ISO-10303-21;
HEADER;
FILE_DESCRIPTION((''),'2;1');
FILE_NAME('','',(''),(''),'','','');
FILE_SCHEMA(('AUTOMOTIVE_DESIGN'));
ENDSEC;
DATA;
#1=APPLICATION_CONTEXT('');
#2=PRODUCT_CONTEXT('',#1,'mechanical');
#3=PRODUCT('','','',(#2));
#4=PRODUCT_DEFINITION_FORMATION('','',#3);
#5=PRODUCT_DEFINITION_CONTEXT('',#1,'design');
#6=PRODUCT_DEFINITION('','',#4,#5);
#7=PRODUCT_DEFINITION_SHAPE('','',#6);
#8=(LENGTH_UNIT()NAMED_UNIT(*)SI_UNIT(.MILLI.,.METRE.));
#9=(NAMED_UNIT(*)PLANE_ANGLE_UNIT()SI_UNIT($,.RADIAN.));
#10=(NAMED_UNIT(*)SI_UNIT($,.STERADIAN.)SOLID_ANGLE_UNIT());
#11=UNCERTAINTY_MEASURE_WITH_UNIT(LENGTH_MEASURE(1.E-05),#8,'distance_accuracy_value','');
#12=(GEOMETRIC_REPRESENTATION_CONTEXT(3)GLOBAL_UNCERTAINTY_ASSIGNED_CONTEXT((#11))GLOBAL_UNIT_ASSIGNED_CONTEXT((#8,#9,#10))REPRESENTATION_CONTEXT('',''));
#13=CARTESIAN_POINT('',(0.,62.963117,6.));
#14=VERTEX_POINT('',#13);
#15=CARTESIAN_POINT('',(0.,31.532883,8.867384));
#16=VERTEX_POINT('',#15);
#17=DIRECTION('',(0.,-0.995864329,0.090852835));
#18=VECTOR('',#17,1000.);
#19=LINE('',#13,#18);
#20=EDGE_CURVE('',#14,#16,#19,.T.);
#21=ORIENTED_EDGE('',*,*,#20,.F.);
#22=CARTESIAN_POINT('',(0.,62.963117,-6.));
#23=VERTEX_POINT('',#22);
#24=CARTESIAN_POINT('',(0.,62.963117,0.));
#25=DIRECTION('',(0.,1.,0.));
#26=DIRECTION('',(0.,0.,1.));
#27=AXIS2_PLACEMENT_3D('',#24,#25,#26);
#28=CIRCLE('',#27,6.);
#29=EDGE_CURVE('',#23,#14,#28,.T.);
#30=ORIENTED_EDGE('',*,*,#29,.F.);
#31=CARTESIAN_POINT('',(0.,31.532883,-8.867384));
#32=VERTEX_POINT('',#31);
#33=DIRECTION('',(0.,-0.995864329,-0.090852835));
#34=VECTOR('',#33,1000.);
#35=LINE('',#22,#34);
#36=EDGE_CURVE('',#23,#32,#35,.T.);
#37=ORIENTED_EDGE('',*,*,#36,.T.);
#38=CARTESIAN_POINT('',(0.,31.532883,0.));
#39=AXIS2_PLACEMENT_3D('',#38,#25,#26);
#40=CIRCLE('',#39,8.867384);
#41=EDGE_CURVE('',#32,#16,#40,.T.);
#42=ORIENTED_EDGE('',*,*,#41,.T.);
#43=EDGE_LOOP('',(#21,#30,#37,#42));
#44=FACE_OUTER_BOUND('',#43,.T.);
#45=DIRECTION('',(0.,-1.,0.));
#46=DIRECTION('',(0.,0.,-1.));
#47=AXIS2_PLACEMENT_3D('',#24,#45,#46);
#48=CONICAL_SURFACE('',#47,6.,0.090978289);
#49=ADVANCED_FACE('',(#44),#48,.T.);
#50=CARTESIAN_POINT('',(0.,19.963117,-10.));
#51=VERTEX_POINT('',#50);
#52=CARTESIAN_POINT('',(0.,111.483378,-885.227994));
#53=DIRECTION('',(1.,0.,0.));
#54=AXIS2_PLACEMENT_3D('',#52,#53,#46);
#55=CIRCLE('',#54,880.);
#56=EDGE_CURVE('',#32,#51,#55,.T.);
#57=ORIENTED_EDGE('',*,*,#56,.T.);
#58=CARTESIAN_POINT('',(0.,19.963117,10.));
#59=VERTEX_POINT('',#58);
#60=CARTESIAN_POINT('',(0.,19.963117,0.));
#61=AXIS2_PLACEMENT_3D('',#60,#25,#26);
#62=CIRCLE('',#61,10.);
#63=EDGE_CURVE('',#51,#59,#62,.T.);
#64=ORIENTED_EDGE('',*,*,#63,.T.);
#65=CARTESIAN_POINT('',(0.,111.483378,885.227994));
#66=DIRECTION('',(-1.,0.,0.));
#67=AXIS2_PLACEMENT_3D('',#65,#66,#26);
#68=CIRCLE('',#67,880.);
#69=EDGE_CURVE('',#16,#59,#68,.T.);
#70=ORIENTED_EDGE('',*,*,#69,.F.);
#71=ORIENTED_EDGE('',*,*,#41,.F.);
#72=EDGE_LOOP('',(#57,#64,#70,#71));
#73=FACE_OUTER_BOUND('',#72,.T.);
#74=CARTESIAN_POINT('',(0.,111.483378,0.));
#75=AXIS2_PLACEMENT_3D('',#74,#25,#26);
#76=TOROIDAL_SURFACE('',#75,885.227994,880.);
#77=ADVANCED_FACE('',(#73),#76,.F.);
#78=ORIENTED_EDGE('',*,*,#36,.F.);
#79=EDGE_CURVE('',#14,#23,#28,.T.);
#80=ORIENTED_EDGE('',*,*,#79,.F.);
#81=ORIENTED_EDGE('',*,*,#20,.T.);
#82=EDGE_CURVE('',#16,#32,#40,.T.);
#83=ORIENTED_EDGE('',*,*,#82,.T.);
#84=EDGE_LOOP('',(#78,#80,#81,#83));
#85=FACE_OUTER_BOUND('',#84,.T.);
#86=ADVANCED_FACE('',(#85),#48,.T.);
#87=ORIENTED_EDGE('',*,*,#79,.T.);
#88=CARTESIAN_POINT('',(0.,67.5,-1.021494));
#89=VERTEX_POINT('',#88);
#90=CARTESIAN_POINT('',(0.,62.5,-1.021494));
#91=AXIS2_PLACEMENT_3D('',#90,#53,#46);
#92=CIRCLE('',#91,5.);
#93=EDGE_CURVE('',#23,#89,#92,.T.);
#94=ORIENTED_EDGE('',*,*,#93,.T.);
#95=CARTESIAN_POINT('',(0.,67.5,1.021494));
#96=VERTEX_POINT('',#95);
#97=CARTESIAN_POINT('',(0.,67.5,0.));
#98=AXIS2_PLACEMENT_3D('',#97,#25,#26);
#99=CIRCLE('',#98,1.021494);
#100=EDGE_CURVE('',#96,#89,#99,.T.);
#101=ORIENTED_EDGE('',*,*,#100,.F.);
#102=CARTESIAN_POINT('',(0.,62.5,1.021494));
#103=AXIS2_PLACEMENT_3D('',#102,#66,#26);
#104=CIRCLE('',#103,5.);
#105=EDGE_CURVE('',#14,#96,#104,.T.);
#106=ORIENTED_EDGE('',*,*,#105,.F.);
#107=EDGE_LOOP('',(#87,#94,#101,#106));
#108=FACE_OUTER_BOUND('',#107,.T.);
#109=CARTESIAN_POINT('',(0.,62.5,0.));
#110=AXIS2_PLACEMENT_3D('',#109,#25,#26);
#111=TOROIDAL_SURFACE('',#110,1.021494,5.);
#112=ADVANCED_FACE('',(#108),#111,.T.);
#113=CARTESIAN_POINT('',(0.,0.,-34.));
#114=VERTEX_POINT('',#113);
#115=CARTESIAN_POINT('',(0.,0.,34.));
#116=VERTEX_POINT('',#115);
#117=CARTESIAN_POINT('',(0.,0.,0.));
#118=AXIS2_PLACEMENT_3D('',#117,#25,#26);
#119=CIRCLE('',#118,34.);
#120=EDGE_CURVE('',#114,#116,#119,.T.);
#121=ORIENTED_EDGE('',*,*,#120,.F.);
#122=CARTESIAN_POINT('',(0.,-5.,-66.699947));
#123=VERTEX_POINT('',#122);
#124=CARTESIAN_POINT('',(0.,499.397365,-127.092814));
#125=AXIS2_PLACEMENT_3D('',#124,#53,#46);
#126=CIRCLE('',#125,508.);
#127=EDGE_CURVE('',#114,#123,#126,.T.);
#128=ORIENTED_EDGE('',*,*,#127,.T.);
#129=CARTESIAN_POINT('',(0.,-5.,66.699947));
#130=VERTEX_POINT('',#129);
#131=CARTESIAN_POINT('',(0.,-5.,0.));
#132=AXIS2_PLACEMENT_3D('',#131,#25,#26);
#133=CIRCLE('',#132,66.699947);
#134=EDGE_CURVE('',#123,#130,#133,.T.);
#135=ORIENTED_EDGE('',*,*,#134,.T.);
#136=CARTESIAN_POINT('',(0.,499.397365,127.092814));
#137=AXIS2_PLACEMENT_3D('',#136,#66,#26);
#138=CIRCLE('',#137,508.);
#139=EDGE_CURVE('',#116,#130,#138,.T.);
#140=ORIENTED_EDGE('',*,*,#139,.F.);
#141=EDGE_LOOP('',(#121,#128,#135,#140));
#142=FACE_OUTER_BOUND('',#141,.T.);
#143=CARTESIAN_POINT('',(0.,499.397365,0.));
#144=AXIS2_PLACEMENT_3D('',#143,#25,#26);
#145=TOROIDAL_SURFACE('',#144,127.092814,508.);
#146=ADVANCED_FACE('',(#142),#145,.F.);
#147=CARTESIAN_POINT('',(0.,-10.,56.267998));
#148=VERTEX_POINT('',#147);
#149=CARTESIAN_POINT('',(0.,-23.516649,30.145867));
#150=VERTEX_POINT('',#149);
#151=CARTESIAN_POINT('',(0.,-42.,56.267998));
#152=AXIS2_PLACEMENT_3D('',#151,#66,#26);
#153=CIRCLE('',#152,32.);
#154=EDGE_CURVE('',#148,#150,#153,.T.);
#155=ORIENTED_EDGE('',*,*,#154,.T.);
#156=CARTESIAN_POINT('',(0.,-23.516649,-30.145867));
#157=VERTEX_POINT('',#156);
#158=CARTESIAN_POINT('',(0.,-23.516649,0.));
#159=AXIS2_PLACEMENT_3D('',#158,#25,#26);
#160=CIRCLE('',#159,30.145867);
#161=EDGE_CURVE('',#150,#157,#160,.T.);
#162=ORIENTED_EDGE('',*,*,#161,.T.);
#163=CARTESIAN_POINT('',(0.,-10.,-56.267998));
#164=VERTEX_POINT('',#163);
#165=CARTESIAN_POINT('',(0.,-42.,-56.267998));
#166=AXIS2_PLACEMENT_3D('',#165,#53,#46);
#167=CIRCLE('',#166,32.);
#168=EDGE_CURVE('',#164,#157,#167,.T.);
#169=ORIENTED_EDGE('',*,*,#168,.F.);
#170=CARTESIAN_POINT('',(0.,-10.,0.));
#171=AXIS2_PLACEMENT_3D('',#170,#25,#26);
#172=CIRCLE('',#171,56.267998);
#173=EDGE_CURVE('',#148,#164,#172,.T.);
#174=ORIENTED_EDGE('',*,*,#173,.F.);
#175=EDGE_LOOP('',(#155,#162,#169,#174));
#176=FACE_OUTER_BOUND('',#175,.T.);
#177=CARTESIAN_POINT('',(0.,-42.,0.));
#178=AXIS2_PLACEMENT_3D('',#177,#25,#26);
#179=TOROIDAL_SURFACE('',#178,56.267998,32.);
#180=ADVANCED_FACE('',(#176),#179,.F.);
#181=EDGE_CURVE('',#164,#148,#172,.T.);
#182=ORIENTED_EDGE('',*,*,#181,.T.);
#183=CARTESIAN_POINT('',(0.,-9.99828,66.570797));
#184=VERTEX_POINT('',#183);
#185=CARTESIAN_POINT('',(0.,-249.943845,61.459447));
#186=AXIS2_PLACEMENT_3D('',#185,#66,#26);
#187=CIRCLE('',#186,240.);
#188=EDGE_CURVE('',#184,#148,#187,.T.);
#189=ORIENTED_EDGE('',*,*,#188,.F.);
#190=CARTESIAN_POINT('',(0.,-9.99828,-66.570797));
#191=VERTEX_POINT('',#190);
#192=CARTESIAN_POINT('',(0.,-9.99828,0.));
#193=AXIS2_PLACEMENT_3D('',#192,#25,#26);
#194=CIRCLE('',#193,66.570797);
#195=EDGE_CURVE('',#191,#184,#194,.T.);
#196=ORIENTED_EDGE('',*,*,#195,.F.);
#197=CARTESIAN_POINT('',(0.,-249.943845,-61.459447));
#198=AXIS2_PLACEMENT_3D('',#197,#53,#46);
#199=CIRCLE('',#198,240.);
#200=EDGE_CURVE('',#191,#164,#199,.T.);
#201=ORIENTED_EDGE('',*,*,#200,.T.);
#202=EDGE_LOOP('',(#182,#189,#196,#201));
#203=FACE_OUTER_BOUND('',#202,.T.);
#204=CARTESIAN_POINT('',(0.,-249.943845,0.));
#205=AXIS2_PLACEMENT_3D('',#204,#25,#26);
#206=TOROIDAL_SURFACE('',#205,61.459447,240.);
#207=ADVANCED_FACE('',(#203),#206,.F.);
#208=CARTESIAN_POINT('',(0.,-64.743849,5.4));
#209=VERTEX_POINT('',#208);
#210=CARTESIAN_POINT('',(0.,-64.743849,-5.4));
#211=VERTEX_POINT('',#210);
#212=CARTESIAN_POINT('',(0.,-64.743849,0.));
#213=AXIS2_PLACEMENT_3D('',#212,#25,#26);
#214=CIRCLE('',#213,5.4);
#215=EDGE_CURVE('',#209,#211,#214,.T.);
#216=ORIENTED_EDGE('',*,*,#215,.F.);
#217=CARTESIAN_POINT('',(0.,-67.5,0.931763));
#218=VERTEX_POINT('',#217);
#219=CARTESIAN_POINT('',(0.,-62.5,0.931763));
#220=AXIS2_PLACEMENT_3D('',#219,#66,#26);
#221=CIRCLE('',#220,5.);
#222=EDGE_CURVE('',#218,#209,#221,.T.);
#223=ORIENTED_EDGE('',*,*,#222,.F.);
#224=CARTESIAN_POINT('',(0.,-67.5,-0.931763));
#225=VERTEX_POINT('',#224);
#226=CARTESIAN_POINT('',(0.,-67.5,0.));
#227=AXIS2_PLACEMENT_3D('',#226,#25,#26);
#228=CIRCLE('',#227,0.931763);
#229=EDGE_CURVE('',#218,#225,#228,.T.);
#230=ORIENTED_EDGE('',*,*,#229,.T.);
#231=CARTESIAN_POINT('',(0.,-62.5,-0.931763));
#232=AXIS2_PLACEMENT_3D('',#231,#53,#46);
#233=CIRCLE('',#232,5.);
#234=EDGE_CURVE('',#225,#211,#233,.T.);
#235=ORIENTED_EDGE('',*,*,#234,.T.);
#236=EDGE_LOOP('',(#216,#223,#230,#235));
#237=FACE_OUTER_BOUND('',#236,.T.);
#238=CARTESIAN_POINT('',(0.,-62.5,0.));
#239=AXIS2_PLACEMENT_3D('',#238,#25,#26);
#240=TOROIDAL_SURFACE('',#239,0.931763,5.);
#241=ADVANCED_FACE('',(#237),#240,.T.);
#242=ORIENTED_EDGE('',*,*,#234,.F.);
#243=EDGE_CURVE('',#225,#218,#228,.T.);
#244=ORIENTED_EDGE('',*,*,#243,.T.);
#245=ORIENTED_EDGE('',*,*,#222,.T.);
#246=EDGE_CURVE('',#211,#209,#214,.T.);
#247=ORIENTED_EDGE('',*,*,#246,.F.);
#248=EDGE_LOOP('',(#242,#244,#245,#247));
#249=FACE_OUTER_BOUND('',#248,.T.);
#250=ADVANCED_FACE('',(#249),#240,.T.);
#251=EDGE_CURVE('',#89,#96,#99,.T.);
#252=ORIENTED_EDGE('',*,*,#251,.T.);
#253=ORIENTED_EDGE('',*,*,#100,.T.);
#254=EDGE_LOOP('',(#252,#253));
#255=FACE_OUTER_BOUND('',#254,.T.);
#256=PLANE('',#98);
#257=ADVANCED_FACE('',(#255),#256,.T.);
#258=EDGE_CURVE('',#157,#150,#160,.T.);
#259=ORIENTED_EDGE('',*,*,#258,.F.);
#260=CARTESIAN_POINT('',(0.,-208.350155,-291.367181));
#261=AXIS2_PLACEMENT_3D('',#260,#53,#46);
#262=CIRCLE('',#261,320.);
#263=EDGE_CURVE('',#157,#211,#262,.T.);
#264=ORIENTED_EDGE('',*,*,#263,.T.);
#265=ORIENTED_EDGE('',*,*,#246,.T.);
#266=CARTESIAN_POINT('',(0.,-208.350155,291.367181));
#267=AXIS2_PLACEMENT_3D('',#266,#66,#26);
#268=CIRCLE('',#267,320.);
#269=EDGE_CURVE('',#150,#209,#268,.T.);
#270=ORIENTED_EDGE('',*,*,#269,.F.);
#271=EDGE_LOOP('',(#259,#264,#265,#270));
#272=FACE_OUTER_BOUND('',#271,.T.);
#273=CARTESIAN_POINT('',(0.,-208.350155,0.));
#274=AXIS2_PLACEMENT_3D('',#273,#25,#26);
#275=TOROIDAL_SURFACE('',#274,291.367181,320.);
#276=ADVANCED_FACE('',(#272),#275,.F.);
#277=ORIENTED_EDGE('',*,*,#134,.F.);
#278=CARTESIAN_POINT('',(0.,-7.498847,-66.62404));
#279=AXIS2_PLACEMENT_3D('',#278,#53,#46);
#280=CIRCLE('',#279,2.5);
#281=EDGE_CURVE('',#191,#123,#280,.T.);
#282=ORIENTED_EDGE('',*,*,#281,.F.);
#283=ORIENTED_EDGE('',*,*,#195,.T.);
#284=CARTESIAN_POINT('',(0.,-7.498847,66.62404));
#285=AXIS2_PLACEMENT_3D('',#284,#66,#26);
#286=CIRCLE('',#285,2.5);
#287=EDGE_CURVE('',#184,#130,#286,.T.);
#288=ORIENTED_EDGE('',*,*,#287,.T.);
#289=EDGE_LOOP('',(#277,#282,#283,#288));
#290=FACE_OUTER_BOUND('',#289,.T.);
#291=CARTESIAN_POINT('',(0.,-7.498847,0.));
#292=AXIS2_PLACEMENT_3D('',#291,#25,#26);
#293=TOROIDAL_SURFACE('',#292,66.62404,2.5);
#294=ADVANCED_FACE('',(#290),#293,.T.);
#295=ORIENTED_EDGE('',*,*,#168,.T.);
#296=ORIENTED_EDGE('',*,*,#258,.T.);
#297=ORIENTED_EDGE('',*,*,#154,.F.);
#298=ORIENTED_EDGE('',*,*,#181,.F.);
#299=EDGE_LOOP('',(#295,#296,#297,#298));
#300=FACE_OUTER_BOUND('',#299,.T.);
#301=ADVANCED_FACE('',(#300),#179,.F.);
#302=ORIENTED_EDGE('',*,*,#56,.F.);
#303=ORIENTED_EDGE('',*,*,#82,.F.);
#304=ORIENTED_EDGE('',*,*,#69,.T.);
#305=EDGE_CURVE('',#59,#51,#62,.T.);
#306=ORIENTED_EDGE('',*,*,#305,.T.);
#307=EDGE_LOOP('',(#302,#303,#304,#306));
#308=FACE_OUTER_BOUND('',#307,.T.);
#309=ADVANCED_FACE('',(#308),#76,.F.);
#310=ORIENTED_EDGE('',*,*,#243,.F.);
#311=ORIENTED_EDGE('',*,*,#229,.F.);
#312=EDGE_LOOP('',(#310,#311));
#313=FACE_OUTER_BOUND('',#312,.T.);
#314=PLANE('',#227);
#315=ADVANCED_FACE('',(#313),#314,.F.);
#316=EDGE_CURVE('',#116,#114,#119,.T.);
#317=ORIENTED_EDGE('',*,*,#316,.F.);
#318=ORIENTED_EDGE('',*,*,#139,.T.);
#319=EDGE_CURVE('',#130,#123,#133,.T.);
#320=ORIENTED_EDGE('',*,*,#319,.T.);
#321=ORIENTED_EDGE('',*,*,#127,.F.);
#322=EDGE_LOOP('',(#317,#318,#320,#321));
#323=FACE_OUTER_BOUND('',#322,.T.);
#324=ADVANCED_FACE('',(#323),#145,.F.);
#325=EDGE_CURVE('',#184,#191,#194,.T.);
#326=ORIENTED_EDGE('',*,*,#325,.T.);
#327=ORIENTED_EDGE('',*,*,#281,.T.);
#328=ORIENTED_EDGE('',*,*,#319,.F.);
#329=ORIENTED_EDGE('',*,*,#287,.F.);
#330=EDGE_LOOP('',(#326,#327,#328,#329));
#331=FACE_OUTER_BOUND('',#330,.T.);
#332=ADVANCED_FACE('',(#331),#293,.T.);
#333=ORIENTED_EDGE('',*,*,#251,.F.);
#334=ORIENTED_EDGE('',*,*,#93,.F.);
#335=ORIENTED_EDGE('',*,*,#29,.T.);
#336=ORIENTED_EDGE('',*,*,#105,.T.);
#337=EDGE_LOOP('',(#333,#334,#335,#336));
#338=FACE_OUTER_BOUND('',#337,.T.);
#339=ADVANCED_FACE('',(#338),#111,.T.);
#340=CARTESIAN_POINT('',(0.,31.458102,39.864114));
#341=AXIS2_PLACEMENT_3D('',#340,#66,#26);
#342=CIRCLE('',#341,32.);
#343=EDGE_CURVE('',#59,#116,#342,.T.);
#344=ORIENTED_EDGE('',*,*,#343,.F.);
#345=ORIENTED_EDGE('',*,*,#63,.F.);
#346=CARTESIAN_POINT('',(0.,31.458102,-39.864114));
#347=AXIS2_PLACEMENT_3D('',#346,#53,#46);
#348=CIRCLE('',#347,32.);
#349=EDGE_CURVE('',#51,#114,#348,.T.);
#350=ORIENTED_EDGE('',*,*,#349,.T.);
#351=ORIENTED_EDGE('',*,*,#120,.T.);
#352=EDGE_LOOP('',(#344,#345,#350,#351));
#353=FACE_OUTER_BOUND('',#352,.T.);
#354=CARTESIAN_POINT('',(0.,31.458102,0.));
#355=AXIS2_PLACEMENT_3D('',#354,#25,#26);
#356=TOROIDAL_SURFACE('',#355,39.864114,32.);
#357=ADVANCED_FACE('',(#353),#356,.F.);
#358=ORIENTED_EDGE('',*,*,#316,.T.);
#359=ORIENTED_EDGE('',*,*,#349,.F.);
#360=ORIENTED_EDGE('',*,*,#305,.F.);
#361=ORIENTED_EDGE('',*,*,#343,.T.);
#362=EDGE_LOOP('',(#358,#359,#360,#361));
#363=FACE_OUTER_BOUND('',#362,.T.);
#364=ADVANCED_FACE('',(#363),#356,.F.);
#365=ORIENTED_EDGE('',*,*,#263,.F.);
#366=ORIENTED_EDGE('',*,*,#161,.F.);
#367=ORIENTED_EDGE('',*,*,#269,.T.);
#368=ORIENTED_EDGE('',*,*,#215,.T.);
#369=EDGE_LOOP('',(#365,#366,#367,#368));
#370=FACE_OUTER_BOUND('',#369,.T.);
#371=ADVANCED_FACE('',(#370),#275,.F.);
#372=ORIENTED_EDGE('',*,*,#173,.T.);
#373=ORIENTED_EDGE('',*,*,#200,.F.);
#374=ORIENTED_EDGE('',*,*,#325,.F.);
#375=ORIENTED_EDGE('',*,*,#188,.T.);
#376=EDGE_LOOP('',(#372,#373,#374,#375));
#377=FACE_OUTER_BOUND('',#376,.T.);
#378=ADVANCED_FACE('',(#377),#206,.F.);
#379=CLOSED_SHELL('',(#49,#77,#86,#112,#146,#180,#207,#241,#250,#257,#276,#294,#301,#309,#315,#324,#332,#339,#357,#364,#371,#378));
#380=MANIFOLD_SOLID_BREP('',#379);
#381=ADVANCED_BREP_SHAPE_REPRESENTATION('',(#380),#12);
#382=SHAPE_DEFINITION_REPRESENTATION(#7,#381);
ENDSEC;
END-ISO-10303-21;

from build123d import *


with BuildPart() as part:
    # Top Half Profile → Spinning Top Revolve (revolve)
    with BuildSketch(Plane.XY, mode=Mode.PRIVATE) as spinning_top_revolve_sk:
        with BuildLine():
            ThreePointArc((66.699946845, -5), (69.123205901, -7.563423043), (66.570796819, -9.998280333))
            ThreePointArc((66.570796819, -9.998280333), (61.41938821, -9.943848556), (56.267998059, -10))
            ThreePointArc((56.267998059, -10), (41.561999586, -13.579345382), (30.145866595, -23.516649444))
            ThreePointArc((30.145866595, -23.516649444), (16.997479936, -43.6647974), (5.4, -64.743848539))
            ThreePointArc((5.4, -64.743848539), (3.55671587, -66.755540077), (0.931762793, -67.5))
            Line((0.931762793, -67.5), (0, -67.5))
            Line((0, -67.5), (0, 67.5))
            Line((0, 67.5), (1.02149392, 67.5))
            ThreePointArc((1.02149392, 67.5), (4.389313376, 66.19564502), (6, 62.963116845))
            Line((6, 62.963116845), (8.867384456, 31.532882589))
            ThreePointArc((8.867384456, 31.532882589), (9.414586997, 25.746129421), (10, 19.963116845))
            ThreePointArc((10, 19.963116845), (19.400534743, 6.856436897), (34, 0))
            ThreePointArc((34, 0), (50.309263809, -2.766240437), (66.699946845, -5))
        make_face()
    revolve(spinning_top_revolve_sk.sketch.rotate(Axis((0, 67.5, 0), (0, -1, 0)), 90), axis=Axis((0, 67.5, 0), (0, -1, 0)))


solid = part.part
